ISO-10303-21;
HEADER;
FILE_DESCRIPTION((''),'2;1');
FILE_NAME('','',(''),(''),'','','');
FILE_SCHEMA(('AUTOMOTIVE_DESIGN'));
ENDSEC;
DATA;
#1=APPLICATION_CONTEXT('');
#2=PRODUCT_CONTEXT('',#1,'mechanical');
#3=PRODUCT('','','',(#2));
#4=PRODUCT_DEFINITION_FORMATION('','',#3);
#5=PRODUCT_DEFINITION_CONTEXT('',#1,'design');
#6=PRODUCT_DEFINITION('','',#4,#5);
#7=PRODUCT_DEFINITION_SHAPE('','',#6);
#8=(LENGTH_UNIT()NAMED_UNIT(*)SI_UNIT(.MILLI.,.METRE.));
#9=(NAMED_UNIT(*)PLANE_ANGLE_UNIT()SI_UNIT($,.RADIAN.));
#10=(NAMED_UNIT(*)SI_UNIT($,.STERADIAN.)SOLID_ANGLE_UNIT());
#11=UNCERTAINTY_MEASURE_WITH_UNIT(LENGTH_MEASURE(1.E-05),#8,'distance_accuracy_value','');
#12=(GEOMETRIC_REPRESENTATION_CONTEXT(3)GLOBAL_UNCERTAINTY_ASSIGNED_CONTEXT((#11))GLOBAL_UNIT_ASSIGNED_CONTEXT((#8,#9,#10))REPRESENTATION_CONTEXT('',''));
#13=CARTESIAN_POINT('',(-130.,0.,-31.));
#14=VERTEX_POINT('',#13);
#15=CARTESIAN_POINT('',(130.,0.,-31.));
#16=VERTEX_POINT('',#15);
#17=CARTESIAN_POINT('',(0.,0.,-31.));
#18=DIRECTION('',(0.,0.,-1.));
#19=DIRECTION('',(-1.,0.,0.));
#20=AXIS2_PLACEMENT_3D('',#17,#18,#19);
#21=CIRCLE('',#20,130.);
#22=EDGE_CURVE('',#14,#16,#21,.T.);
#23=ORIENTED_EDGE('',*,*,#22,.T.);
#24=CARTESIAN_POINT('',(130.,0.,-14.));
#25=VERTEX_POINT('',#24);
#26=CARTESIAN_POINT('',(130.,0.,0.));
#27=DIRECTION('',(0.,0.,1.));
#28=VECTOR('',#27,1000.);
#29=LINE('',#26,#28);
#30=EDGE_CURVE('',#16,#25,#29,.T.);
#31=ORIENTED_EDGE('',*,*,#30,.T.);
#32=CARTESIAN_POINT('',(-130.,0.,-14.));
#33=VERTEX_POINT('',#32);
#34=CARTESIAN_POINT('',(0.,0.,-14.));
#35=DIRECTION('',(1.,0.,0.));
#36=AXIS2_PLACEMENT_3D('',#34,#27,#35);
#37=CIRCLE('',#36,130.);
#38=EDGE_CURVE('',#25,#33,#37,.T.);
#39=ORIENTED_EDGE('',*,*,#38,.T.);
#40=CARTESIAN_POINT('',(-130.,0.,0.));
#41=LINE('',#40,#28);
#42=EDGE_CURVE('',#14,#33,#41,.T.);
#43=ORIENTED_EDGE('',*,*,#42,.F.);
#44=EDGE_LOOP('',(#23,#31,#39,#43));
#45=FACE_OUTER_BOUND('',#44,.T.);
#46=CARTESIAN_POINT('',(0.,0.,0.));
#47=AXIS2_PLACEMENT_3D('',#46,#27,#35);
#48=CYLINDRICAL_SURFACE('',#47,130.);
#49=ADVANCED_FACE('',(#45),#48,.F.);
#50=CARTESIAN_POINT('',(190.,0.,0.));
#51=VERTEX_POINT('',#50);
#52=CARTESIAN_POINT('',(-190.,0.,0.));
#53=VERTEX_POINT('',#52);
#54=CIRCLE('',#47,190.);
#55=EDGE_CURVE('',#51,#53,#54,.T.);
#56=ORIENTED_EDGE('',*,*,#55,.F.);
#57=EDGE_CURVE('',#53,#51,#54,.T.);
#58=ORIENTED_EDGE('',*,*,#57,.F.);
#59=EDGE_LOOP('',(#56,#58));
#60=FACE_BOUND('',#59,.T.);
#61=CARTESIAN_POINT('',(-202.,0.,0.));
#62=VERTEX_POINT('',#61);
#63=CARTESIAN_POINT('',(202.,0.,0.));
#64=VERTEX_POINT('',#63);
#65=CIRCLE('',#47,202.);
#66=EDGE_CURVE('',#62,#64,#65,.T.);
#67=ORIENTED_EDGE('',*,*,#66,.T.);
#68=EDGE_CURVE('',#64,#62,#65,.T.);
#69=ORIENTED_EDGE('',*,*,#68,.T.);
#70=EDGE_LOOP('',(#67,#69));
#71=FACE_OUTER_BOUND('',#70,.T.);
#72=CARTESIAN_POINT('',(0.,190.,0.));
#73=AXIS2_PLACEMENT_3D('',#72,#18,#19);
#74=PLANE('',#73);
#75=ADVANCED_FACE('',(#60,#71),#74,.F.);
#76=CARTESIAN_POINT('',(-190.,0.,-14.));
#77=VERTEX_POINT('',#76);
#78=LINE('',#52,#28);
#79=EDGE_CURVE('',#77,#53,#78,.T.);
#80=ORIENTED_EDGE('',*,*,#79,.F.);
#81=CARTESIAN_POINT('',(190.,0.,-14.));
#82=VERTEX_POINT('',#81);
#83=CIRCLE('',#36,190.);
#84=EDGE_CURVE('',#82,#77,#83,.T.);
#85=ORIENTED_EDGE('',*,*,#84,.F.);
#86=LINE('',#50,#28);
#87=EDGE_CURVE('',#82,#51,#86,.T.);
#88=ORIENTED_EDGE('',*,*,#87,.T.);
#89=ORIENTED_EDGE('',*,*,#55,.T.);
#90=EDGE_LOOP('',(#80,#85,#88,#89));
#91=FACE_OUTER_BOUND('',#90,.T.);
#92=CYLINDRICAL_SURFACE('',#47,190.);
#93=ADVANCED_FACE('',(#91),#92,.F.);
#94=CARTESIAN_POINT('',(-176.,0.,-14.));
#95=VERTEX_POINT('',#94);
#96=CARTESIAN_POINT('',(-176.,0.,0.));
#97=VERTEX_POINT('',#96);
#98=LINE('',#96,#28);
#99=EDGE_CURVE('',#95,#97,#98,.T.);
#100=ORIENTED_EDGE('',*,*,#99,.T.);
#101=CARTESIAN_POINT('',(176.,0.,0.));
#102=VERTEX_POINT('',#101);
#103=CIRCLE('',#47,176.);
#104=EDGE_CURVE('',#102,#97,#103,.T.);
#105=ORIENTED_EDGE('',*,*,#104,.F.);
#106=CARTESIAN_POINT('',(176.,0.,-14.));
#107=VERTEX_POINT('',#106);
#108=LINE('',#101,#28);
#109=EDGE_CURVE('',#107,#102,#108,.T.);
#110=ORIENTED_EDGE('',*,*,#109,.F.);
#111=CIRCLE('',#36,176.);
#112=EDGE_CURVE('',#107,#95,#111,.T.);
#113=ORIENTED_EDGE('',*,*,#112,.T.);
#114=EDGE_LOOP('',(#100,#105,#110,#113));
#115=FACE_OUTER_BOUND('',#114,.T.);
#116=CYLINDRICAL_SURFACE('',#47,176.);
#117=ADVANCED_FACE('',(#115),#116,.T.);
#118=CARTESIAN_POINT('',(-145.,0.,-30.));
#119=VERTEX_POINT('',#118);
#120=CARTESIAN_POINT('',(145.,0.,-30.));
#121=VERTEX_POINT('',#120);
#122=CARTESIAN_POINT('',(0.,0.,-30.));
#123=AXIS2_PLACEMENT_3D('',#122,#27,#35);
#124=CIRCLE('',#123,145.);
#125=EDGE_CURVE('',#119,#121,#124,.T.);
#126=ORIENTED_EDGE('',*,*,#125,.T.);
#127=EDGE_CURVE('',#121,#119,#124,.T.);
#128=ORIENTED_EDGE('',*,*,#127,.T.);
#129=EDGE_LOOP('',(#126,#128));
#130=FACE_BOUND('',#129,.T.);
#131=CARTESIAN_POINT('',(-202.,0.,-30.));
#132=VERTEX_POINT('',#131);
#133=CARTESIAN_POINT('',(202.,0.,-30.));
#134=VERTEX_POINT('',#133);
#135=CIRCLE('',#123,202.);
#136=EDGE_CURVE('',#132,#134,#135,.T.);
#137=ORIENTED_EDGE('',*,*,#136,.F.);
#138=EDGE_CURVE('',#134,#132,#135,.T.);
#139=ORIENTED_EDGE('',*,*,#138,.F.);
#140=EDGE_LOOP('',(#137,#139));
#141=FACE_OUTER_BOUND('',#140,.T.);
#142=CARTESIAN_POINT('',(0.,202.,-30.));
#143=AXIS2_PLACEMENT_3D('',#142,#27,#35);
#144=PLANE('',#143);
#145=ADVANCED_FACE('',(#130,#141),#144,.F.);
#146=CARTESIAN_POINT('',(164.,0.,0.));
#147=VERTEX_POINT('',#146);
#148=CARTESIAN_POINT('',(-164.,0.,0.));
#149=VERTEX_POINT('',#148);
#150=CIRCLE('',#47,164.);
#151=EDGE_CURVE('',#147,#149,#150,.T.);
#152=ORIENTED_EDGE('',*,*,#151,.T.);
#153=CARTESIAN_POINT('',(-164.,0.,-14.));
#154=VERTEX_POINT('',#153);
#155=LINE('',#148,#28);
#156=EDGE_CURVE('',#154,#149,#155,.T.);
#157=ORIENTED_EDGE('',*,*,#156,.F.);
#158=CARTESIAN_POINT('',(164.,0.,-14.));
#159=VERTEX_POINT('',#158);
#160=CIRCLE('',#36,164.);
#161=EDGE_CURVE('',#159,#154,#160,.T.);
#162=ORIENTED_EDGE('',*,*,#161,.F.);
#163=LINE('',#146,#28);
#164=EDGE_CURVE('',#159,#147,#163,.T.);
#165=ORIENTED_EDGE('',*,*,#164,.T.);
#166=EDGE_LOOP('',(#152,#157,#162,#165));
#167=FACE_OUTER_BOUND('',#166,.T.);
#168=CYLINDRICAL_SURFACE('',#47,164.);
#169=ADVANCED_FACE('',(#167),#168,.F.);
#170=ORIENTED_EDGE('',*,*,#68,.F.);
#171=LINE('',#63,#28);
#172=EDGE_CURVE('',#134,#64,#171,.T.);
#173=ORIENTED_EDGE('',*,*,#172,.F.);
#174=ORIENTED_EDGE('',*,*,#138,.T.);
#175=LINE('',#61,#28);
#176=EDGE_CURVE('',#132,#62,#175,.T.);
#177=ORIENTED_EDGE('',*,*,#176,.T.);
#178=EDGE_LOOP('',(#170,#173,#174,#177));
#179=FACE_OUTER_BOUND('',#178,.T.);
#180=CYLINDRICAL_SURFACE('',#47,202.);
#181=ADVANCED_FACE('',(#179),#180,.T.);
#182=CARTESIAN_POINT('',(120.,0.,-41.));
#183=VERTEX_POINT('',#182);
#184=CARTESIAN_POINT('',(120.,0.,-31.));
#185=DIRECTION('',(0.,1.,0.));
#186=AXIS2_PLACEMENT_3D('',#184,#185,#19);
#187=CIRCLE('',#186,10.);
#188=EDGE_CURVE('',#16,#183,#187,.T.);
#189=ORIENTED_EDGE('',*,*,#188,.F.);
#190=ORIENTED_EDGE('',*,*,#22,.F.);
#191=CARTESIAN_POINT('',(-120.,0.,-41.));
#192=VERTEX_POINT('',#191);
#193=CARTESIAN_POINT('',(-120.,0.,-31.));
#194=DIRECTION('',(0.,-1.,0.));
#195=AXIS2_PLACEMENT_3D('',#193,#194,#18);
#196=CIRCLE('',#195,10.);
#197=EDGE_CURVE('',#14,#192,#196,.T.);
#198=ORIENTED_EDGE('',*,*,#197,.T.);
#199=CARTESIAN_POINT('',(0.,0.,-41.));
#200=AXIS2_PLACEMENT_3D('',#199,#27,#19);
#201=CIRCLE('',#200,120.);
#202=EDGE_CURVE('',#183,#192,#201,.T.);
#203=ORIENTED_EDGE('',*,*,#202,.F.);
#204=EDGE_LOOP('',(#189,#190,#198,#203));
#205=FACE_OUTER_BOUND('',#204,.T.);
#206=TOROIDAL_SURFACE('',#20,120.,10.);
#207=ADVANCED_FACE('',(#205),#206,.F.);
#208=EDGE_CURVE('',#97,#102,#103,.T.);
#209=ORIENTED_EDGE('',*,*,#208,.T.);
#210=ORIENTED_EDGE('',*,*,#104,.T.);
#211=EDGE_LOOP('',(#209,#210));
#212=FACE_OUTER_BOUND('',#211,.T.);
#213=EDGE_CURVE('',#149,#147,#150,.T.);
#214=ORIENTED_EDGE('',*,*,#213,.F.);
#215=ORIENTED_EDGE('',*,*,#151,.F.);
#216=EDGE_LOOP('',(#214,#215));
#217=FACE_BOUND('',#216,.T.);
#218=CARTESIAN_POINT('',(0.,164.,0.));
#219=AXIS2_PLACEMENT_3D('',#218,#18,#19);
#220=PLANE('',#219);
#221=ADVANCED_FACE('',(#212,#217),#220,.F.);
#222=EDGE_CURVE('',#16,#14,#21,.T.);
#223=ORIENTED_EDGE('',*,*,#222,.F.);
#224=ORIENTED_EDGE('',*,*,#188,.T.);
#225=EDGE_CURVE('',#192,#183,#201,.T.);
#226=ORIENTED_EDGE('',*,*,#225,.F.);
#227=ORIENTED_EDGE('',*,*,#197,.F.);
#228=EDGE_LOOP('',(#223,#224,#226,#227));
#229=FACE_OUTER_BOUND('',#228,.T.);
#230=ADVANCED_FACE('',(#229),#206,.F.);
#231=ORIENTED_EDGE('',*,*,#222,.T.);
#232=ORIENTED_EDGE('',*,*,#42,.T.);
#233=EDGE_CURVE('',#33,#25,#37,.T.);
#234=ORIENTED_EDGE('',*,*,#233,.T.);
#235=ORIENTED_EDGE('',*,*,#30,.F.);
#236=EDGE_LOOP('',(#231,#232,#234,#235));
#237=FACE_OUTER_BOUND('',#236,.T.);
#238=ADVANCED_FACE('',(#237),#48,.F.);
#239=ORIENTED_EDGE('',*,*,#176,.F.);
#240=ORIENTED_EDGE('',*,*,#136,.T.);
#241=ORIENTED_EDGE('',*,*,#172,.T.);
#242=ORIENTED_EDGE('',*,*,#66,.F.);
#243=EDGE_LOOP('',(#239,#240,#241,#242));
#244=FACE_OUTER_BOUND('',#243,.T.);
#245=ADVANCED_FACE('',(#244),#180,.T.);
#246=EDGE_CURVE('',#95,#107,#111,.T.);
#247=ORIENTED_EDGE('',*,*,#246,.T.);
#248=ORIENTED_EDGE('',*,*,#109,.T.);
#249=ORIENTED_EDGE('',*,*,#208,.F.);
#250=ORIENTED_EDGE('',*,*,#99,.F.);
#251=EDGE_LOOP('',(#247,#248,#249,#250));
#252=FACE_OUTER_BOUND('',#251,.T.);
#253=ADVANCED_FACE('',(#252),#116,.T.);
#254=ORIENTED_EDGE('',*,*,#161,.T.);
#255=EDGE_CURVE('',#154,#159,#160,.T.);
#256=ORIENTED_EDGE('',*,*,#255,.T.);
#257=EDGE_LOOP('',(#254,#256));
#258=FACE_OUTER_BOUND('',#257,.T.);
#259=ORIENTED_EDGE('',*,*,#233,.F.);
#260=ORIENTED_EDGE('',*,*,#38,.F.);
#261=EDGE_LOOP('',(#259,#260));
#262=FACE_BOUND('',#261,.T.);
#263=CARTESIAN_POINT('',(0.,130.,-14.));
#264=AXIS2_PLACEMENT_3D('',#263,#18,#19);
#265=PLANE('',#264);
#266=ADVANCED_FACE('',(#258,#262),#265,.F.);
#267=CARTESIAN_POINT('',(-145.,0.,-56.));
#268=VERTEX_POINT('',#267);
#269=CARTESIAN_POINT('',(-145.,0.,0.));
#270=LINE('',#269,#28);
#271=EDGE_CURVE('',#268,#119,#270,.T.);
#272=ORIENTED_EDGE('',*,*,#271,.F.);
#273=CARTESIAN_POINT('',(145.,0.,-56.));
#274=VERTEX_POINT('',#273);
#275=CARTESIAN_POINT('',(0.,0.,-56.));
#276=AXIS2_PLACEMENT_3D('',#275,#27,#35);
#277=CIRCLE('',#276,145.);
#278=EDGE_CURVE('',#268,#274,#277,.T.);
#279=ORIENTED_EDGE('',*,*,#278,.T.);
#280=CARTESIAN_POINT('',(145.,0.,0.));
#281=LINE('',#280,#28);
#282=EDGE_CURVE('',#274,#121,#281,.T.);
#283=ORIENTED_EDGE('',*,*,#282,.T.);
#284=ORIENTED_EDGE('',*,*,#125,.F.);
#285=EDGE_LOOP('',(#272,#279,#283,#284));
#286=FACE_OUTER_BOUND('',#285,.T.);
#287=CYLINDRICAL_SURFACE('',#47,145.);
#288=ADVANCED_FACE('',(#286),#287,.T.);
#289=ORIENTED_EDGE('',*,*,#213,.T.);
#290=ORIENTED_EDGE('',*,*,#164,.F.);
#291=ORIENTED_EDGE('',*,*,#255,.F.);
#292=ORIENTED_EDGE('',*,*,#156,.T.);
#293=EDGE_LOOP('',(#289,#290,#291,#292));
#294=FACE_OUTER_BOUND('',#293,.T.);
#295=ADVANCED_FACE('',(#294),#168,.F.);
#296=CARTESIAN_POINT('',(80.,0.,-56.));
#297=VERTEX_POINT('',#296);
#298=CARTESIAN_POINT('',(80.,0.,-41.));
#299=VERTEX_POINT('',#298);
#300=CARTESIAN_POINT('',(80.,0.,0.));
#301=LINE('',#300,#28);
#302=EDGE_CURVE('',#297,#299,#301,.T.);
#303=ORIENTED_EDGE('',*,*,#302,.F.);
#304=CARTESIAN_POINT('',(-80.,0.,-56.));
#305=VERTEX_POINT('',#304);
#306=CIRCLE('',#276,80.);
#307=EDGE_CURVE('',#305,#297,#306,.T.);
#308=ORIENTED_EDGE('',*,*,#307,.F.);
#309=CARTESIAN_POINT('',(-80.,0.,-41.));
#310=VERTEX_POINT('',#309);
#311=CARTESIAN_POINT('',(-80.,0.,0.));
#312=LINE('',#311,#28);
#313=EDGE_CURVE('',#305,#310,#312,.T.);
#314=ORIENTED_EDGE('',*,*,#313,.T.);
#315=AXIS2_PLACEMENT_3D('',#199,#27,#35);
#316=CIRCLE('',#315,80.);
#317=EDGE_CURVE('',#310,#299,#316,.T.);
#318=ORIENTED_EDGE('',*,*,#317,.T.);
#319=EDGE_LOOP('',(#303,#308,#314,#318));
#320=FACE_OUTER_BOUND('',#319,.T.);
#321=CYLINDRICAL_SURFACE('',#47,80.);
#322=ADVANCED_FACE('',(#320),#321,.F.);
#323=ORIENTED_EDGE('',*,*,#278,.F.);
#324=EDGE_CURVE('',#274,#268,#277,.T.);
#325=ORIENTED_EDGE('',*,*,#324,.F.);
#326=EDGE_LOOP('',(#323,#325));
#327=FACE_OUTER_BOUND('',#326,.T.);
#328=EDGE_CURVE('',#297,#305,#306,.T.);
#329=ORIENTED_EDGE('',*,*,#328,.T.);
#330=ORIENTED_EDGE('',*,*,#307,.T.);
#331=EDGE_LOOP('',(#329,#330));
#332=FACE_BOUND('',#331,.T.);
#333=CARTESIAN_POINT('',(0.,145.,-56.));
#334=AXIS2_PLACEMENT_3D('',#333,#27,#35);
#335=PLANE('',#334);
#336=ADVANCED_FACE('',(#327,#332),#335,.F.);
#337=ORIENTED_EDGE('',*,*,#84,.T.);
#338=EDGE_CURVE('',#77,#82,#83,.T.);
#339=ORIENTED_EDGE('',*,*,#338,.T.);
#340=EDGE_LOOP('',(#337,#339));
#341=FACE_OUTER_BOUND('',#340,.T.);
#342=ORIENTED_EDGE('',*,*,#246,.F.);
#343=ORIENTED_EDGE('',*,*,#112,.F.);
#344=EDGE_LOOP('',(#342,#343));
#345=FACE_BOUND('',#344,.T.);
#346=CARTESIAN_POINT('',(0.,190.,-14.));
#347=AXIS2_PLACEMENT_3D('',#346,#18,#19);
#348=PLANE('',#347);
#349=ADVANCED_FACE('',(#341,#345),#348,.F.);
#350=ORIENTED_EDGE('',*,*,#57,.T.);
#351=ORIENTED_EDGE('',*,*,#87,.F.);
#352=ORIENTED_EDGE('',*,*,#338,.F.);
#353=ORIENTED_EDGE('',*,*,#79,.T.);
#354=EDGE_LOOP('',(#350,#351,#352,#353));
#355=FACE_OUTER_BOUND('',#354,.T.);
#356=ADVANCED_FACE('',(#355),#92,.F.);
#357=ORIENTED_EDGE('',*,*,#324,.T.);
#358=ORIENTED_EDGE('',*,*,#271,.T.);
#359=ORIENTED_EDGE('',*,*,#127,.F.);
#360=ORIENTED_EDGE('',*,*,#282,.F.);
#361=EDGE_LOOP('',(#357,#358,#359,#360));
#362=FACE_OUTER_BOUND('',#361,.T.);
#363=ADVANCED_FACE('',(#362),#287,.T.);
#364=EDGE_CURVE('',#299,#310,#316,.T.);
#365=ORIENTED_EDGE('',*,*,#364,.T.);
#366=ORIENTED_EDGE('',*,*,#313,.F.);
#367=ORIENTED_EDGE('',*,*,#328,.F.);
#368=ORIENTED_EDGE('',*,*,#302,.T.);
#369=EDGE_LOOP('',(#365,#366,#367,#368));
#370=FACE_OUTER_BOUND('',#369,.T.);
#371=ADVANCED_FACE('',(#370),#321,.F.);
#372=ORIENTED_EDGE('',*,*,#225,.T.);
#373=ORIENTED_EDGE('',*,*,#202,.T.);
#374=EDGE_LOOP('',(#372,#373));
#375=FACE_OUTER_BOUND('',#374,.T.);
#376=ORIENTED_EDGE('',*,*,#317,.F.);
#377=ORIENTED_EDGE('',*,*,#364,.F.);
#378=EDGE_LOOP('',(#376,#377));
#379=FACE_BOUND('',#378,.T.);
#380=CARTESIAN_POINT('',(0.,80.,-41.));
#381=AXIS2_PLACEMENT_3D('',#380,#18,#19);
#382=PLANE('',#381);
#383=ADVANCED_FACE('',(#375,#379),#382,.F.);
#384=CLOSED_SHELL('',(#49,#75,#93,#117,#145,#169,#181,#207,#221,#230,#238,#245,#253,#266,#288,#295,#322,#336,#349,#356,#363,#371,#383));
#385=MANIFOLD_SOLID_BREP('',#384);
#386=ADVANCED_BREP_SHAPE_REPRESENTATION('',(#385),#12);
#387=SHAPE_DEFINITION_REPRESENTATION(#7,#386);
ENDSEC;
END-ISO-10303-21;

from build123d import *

# Parameters (mm, degrees)
FILLET1_R = 10


with BuildPart() as part:
    # Sketch1 → Revolve1 (revolve)
    with BuildSketch(Plane(origin=(0, 0, 0), x_dir=(0, 0, -1), z_dir=(1, 0, 0)), mode=Mode.PRIVATE) as revolve1_sk:
        Polygon((0, 164), (0, 176), (14, 176), (14, 190), (0, 190), (0, 202), (30, 202), (30, 145), (56, 145), (56, 80), (41, 80), (41, 130), (14, 130), (14, 164), align=None)
    revolve(revolve1_sk.sketch.rotate(Axis((0, 0, 0), (0, 0, -1)), 90), axis=Axis((0, 0, 0), (0, 0, -1)))

    # Fillet1
    fillet1_edges = [part.edges().sort_by_distance(p)[0] for p in [
        (-130, 0, -41),
    ]]
    fillet(fillet1_edges, radius=FILLET1_R)


solid = part.part
